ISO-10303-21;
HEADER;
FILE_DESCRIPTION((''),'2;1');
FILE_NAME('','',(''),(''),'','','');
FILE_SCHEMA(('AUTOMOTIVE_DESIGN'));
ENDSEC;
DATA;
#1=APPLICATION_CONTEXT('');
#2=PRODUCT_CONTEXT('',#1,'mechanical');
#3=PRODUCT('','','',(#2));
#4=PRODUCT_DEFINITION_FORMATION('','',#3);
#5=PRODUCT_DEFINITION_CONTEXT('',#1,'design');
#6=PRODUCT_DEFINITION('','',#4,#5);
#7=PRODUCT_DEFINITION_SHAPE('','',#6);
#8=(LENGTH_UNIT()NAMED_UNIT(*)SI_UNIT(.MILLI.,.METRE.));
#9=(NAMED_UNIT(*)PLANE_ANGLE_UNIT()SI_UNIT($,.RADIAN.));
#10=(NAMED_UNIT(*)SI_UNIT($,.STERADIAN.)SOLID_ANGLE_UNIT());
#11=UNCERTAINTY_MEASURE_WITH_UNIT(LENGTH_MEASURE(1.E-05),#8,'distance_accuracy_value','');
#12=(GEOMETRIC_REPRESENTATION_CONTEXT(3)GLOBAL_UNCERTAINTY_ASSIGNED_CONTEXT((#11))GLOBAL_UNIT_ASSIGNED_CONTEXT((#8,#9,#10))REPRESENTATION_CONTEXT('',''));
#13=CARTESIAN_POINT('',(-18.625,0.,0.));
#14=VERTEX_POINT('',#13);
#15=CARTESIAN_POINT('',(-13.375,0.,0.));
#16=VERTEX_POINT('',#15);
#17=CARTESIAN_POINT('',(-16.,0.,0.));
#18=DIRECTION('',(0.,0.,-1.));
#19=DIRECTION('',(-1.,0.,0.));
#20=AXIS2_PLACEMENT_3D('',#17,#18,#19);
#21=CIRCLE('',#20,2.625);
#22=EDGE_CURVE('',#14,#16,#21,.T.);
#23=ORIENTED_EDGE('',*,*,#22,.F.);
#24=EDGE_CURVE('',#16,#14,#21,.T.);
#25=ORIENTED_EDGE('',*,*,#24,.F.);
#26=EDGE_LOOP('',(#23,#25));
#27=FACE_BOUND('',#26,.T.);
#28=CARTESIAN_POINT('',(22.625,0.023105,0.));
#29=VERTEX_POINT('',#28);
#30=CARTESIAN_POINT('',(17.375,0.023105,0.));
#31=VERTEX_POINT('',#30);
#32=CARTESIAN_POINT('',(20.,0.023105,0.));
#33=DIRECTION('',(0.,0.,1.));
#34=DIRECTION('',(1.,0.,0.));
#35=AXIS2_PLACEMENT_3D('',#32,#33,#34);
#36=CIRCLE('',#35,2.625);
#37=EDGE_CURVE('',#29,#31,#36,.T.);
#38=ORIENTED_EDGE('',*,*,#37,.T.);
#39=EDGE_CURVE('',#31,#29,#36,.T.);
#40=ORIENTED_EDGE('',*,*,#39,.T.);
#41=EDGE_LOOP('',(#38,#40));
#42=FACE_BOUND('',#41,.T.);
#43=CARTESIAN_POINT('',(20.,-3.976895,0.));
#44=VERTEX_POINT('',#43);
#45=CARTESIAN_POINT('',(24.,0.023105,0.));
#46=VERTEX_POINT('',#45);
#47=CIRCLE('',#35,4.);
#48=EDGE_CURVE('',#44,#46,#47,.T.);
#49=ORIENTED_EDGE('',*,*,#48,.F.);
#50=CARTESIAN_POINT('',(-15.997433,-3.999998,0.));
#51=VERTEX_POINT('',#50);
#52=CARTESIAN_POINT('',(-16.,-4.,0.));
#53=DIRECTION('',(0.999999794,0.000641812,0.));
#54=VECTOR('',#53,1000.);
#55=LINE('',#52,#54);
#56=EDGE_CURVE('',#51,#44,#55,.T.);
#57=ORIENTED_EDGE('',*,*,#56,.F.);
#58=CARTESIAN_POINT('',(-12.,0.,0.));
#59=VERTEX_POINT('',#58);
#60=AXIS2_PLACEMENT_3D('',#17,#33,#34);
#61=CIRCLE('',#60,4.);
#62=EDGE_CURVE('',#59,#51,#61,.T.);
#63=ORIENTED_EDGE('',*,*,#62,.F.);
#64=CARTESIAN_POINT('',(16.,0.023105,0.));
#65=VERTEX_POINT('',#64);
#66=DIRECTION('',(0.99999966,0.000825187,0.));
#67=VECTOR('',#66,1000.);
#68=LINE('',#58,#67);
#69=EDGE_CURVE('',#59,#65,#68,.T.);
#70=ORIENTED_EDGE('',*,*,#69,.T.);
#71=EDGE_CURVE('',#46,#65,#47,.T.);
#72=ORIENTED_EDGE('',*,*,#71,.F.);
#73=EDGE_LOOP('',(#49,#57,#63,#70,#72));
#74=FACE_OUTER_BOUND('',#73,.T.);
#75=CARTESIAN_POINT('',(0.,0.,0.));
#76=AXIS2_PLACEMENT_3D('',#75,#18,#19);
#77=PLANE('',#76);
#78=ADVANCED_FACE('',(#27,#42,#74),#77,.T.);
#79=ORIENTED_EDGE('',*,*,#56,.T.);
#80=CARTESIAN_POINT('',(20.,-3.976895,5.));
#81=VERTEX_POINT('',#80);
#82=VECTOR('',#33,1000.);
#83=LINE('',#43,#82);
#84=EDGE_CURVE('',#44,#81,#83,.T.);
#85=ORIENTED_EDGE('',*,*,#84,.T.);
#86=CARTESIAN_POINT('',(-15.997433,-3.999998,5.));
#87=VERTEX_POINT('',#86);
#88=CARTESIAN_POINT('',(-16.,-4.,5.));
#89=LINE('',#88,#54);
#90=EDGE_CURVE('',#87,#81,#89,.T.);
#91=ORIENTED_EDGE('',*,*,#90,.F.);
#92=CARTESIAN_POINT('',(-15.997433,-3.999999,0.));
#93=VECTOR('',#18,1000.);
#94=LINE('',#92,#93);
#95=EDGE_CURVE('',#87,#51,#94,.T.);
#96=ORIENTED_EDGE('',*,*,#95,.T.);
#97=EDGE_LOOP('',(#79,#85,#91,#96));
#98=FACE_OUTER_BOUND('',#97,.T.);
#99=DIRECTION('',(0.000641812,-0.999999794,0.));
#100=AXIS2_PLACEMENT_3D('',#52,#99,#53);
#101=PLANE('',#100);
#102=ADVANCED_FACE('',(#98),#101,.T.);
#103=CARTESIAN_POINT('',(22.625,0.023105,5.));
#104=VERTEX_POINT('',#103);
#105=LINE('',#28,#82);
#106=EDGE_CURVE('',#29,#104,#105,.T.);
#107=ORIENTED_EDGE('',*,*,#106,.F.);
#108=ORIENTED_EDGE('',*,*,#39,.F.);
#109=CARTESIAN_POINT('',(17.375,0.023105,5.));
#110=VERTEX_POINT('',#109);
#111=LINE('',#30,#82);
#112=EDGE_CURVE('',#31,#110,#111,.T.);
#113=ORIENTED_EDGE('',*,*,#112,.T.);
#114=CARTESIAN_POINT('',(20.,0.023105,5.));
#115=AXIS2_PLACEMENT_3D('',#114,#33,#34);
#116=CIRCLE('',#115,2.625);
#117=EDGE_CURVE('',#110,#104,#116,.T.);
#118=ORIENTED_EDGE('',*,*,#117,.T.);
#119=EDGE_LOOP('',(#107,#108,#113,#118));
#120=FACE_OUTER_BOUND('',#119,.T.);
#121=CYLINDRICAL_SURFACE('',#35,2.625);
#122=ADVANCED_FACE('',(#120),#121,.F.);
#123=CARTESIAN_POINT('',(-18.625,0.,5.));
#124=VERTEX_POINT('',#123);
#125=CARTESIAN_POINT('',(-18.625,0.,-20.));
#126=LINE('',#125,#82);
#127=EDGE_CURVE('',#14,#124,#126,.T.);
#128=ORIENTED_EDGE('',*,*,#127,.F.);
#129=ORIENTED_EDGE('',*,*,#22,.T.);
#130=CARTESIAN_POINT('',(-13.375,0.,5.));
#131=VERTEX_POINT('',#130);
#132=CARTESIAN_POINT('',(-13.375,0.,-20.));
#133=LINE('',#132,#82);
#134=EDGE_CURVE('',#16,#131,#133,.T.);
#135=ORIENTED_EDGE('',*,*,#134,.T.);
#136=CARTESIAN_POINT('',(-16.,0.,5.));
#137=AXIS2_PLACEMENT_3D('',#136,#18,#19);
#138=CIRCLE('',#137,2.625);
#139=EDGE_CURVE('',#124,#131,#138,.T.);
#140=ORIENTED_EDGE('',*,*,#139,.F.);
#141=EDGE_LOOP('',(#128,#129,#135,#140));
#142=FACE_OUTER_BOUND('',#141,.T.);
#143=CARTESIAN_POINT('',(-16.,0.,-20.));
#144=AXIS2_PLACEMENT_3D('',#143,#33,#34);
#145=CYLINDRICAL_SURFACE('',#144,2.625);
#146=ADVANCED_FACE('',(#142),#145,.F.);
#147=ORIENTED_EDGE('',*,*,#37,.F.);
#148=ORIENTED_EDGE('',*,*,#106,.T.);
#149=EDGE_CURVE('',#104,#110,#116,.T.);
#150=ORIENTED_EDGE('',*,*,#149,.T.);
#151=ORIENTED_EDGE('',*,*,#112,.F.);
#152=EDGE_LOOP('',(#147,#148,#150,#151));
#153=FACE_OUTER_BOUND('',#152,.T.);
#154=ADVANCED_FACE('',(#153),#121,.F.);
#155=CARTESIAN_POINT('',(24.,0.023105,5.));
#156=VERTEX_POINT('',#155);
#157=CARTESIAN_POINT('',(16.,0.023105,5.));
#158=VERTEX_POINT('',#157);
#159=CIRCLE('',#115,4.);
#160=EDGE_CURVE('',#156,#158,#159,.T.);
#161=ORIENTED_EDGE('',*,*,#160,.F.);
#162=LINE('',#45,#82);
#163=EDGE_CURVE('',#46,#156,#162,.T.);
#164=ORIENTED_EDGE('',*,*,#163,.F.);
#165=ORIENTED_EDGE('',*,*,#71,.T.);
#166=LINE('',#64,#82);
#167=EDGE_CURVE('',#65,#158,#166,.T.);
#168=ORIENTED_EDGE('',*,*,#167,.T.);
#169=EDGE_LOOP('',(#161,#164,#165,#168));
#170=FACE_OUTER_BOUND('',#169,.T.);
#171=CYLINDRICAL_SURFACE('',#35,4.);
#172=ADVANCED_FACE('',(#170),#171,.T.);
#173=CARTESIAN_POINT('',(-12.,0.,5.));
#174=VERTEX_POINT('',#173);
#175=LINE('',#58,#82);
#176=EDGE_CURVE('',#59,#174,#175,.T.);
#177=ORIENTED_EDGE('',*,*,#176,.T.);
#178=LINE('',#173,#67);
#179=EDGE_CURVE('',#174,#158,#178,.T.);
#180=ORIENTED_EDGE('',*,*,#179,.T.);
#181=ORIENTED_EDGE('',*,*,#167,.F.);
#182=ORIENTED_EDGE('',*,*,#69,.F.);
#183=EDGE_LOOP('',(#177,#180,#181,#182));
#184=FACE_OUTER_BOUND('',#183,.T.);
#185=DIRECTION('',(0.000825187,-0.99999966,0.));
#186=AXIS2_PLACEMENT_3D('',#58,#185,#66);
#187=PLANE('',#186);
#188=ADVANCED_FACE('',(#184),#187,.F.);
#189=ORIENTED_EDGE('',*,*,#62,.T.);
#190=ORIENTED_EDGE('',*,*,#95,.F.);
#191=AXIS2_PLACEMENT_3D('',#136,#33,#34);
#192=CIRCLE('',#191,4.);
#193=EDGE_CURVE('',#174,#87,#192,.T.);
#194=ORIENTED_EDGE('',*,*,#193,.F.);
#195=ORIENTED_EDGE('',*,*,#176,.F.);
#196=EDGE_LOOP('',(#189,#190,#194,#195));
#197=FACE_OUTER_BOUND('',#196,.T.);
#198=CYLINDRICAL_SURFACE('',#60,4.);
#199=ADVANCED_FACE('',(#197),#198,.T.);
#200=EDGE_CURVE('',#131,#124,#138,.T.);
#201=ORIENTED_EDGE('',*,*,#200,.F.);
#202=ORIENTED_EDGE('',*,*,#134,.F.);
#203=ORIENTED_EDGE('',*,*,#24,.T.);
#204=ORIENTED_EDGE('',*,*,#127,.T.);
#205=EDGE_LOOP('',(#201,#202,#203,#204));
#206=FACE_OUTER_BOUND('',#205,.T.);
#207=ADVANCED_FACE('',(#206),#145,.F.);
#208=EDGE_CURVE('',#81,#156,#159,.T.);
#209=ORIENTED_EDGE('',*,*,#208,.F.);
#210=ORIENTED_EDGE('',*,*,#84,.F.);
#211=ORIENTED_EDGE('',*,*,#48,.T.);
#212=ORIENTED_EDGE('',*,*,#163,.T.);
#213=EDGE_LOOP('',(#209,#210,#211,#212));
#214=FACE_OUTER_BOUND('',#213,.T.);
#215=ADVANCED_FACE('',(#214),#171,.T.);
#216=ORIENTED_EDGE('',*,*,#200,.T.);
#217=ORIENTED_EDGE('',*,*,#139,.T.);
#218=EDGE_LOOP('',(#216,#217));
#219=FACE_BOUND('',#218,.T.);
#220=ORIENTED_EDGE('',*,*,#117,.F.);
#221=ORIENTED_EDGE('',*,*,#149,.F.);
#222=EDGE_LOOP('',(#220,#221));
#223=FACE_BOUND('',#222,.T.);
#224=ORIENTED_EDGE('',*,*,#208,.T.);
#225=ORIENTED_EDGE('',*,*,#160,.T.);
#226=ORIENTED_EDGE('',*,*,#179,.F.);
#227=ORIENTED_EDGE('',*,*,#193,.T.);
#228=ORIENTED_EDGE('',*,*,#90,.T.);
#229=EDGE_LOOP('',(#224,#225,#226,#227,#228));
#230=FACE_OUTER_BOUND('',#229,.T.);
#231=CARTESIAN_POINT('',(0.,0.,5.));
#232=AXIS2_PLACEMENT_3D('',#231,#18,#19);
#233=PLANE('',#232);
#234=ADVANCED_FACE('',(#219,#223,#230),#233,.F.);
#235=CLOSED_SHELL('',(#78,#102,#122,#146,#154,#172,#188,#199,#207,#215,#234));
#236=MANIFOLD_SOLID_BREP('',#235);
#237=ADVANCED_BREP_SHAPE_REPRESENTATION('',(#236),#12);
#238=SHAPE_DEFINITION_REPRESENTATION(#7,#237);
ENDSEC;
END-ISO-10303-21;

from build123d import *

# Parameters (mm, degrees)
SKETCH1_W            = 35
SKETCH1_H            = 5
BOSS_EXTRUDE3_DEPTH  = 5
SKETCH7_W            = 5
SKETCH7_H            = 5
BOSS_EXTRUDE6_DEPTH  = 5
FILLET6_R            = 1
FILLET7_R            = 1
SKETCH11_R           = 2
CUT_EXTRUDE2_DEPTH   = 5
SKETCH5_R            = 2.375
BOSS_EXTRUDE9_DEPTH  = 5
SKETCH13_R           = 4
BOSS_EXTRUDE10_DEPTH = 5
SKETCH14_R           = 2.625
CUT_EXTRUDE3_DEPTH   = 25.84321589
SKETCH15_W           = 5
SKETCH15_H           = 5
BOSS_EXTRUDE11_DEPTH = 0.875
FILLET8_R            = 2
FILLET9_R            = 2
SKETCH16_R           = 4
BOSS_EXTRUDE12_DEPTH = 5
SKETCH17_R           = 2.625
CUT_EXTRUDE4_DEPTH   = 30
CUT_EXTRUDE5_DEPTH   = 25.84321589
BOSS_EXTRUDE13_DEPTH = 5


with BuildPart() as part:
    # Sketch1 → Boss-Extrude3 (new body)
    with BuildSketch(Plane.XY):
        Rectangle(SKETCH1_W, SKETCH1_H)
    extrude(amount=BOSS_EXTRUDE3_DEPTH)

    # Sketch7 → Boss-Extrude6 (add)
    with BuildSketch(Plane.XY.offset(5)):
        with Locations((20, 0.046210476)):
            Rectangle(SKETCH7_W, SKETCH7_H)
    extrude(amount=-BOSS_EXTRUDE6_DEPTH)

    # Fillet6
    fillet6_edges = [part.edges().sort_by_distance(p)[0] for p in [
        (22.5, 2.546210476, 2.5),
    ]]
    fillet(fillet6_edges, radius=FILLET6_R)

    # Fillet7
    fillet7_edges = [part.edges().sort_by_distance(p)[0] for p in [
        (22.5, -2.453789524, 2.5),
    ]]
    fillet(fillet7_edges, radius=FILLET7_R)

    # Sketch11 → Cut-Extrude2 (cut)
    with BuildSketch(Plane.XY.offset(5)):
        with Locations((20, 0.023105238)):
            Circle(SKETCH11_R)
    extrude(amount=-CUT_EXTRUDE2_DEPTH, mode=Mode.SUBTRACT)

    # Sketch5 → Boss-Extrude9 (add)
    with BuildSketch(Plane.XY.offset(5)):
        with Locations(Location((-16, 0, 0), (0, 0, 230.833289284))):
            Circle(SKETCH5_R)
    extrude(amount=BOSS_EXTRUDE9_DEPTH)

    # Sketch13 → Boss-Extrude10 (add, through all)
    with BuildSketch(Plane.XY.offset(5)):
        with Locations((20, 0.023105238)):
            Circle(SKETCH13_R)
    extrude(amount=-BOSS_EXTRUDE10_DEPTH)

    # Sketch14 → Cut-Extrude3 (cut, through all)
    with BuildSketch(Plane.XY.offset(5)):
        with Locations((20, 0.023105238)):
            Circle(SKETCH14_R)
    extrude(amount=-CUT_EXTRUDE3_DEPTH, mode=Mode.SUBTRACT)

    # Sketch15 → Boss-Extrude11 (add, through all)
    with BuildSketch(Plane.ZY.offset(17.5)):
        with Locations((2.5, 0)):
            Rectangle(SKETCH15_W, SKETCH15_H)
    extrude(amount=BOSS_EXTRUDE11_DEPTH)

    # Fillet8
    fillet8_edges = [part.edges().sort_by_distance(p)[0] for p in [
        (-18.375, 2.5, 2.5),
    ]]
    fillet(fillet8_edges, radius=FILLET8_R)

    # Fillet9
    fillet9_edges = [part.edges().sort_by_distance(p)[0] for p in [
        (-18.375, -2.5, 2.5),
    ]]
    fillet(fillet9_edges, radius=FILLET9_R)

    # Sketch16 → Boss-Extrude12 (add)
    with BuildSketch(Plane.XY.offset(5)):
        with Locations((-16, 0)):
            Circle(SKETCH16_R)
    extrude(amount=-BOSS_EXTRUDE12_DEPTH)

    # Sketch17 → Cut-Extrude4 (cut)
    with BuildSketch(Plane.XY.offset(10)):
        with Locations(Location((-16, 0, 0), (0, 0, 180))):
            Circle(SKETCH17_R)
    extrude(amount=-CUT_EXTRUDE4_DEPTH, mode=Mode.SUBTRACT)

    # Sketch18 → Cut-Extrude5 (cut, through all)
    with BuildSketch(Plane.XY.offset(5)):
        with BuildLine():
            Line((-12, 0), (16, 0.023105238))
            ThreePointArc((16, 0.023105238), (17.170665329, 2.850624525), (19.99743266, 4.023104414))
            Line((19.99743266, 4.023104414), (-16, 4))
            ThreePointArc((-16, 4), (-13.171572875, 2.828427125), (-12, 0))
        make_face()
    extrude(amount=-CUT_EXTRUDE5_DEPTH, mode=Mode.SUBTRACT)

    # Sketch19 → Boss-Extrude13 (add, through all)
    with BuildSketch(Plane.XY.offset(5)):
        Polygon((-16, -4), (20, -3.976894762), (16, -1.273335264), (-12.878635235, -1.649219819), align=None)
    extrude(amount=-BOSS_EXTRUDE13_DEPTH)


solid = part.part
